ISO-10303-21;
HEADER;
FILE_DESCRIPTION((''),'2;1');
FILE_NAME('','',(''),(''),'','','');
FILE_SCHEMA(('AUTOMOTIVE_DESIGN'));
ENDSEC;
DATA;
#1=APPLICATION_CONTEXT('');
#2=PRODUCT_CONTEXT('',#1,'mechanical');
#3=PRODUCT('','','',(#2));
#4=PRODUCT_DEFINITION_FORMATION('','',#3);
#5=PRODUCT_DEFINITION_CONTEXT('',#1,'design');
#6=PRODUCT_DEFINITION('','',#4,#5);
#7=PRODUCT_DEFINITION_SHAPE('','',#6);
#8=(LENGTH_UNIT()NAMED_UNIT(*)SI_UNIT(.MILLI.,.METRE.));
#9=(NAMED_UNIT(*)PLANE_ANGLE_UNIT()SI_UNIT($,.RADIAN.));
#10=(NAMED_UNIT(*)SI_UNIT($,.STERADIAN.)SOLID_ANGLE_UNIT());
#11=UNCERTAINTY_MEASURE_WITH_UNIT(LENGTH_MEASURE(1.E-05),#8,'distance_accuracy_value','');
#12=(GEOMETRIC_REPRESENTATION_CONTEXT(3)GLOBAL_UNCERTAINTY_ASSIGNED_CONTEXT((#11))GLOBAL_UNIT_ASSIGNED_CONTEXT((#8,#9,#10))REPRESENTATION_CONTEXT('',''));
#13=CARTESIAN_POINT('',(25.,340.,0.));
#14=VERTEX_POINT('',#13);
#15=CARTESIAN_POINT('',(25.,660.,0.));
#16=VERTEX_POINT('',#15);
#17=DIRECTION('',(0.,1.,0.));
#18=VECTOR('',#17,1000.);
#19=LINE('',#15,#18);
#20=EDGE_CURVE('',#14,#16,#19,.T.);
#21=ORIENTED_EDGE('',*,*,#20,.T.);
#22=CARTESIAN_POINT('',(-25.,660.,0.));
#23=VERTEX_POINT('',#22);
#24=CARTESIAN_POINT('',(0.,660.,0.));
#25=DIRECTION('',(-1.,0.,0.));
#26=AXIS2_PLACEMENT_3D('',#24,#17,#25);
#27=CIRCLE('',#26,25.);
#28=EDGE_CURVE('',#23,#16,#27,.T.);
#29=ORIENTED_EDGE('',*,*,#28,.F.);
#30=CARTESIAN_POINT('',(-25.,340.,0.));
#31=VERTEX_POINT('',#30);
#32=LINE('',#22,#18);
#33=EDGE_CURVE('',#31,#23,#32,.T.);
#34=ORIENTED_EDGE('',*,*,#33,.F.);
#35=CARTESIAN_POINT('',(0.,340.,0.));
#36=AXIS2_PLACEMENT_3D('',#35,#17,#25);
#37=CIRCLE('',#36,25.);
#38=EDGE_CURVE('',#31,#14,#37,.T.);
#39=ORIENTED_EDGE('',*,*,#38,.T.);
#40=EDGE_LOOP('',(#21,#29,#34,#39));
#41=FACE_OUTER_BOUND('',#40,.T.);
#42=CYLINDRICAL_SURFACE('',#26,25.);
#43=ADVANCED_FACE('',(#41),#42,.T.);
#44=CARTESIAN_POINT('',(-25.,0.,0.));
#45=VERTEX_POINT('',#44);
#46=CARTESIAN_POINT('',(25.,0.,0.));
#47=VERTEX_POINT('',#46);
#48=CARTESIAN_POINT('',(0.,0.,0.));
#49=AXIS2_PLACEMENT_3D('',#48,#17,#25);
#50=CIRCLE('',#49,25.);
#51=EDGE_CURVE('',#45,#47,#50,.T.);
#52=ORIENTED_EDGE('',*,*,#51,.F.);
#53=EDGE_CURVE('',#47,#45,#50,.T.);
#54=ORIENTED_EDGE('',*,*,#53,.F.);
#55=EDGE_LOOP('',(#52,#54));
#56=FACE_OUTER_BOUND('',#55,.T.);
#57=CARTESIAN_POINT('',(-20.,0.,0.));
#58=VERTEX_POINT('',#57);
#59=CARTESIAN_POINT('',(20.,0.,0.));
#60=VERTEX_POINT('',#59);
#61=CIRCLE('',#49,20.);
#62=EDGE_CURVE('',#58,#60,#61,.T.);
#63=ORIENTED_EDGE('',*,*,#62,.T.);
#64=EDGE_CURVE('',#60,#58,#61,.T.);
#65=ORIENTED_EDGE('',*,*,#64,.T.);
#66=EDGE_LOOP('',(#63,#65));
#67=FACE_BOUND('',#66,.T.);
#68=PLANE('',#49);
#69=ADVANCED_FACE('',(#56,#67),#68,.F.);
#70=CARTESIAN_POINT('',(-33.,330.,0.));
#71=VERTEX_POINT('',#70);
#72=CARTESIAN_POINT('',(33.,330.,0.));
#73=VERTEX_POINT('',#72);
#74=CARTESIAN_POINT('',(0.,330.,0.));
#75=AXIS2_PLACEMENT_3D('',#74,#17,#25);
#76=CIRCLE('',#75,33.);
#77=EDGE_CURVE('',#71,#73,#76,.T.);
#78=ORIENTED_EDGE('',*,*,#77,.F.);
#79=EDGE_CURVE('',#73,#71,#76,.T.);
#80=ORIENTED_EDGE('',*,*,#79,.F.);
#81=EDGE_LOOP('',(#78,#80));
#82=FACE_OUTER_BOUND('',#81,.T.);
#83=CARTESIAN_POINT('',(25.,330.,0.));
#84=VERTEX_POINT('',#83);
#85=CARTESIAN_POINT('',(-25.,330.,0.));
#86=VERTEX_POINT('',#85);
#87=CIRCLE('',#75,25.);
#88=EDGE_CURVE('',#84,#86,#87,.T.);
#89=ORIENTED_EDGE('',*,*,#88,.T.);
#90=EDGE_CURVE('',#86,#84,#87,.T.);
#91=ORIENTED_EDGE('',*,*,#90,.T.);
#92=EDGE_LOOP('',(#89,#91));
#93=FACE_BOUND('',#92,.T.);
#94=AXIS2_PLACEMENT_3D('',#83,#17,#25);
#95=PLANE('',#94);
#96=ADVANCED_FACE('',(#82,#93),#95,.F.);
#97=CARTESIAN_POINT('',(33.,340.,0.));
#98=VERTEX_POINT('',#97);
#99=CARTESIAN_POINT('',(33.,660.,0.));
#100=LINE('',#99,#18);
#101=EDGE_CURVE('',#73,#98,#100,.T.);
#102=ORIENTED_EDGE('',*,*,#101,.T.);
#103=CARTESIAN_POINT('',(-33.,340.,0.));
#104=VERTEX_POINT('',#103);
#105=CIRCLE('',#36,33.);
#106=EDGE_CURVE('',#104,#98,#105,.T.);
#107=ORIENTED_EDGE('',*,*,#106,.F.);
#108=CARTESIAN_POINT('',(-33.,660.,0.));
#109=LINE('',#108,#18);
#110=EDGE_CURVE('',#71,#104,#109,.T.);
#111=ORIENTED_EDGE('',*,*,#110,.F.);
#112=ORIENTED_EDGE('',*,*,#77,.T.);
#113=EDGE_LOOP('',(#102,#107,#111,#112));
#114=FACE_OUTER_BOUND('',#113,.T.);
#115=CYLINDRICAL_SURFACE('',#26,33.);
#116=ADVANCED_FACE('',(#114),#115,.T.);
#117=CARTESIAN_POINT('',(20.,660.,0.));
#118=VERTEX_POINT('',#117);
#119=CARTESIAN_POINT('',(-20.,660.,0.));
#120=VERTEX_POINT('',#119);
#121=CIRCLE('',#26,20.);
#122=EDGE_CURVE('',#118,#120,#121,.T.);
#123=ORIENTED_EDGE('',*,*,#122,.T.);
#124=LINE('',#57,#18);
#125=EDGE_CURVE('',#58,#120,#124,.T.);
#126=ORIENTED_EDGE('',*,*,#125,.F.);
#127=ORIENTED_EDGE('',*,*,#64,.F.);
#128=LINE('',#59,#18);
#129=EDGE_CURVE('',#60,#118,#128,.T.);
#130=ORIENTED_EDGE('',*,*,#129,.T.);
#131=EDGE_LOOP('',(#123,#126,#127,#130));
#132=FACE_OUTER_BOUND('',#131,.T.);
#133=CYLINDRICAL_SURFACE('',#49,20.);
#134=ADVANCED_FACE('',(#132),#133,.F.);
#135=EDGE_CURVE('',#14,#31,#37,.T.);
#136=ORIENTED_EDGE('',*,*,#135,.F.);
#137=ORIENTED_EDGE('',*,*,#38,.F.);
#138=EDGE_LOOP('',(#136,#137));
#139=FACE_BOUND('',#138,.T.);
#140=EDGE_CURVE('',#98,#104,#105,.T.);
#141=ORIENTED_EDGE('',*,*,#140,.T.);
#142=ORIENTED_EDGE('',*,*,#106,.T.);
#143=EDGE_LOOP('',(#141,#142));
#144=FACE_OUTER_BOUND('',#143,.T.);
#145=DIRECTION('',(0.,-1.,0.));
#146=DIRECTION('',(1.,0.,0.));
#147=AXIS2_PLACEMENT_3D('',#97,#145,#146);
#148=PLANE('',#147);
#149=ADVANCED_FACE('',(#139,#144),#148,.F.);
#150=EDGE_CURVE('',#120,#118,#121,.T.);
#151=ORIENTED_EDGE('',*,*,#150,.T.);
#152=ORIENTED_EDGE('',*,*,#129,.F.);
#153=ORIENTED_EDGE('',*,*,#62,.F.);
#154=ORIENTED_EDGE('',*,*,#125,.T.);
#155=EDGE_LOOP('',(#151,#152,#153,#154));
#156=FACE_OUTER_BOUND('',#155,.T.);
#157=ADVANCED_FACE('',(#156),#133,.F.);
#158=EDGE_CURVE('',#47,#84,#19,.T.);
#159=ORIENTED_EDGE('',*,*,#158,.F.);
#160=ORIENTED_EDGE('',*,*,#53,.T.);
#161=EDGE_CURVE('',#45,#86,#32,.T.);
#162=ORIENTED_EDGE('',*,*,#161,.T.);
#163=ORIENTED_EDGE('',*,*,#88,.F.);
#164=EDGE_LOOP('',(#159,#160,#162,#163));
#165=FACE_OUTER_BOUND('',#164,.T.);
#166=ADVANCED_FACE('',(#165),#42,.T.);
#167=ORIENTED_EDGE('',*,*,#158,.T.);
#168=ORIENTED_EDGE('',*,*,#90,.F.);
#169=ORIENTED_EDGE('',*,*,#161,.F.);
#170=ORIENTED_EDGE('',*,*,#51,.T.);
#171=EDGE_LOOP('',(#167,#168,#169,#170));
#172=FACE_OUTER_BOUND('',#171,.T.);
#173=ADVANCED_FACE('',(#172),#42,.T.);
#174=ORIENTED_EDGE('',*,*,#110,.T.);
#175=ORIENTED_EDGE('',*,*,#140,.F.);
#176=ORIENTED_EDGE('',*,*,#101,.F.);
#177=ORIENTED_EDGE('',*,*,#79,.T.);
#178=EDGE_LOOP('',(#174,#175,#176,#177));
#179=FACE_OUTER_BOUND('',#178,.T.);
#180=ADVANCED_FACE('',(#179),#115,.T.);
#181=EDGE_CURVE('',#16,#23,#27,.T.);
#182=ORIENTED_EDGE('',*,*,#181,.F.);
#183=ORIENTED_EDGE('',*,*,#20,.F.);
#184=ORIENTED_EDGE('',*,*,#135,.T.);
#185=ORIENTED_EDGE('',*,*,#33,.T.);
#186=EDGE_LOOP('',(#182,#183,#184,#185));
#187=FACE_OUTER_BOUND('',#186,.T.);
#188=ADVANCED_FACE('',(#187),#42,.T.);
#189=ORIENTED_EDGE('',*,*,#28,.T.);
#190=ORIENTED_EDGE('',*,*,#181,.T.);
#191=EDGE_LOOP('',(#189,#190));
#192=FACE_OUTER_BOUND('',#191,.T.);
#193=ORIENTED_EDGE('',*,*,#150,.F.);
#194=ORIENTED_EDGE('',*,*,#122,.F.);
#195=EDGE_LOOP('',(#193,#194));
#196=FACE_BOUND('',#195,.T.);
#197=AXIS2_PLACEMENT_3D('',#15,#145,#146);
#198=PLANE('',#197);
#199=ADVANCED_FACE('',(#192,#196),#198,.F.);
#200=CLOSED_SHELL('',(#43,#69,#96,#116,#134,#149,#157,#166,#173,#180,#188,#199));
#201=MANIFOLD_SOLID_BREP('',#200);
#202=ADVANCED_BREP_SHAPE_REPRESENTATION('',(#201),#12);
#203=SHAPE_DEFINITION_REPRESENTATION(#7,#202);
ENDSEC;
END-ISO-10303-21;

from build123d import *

# Parameters (mm, degrees)
SKETCH2_R          = 20
CUT_EXTRUDE1_DEPTH = 662.64794264


with BuildPart() as part:
    # Sketch1 → Revolve1 (revolve)
    with BuildSketch(Plane.XY, mode=Mode.PRIVATE) as revolve1_sk:
        Polygon((0, 0), (25, 0), (25, 330), (33, 330), (33, 340), (25, 340), (25, 585.119663834), (25, 619.032357738), (25, 660), (0, 660), align=None)
    revolve(revolve1_sk.sketch.rotate(Axis((0, 660, 0), (0, -1, 0)), 180), axis=Axis((0, 660, 0), (0, -1, 0)))

    # Sketch2 → Cut-Extrude1 (cut, through all)
    with BuildSketch(Plane(origin=(0, 660, 0), x_dir=(1, 0, 0), z_dir=(0, 1, 0))):
        with Locations(Location((0, 0, 0), (0, 0, 180))):
            Circle(SKETCH2_R)
    extrude(amount=-CUT_EXTRUDE1_DEPTH, mode=Mode.SUBTRACT)


solid = part.part
